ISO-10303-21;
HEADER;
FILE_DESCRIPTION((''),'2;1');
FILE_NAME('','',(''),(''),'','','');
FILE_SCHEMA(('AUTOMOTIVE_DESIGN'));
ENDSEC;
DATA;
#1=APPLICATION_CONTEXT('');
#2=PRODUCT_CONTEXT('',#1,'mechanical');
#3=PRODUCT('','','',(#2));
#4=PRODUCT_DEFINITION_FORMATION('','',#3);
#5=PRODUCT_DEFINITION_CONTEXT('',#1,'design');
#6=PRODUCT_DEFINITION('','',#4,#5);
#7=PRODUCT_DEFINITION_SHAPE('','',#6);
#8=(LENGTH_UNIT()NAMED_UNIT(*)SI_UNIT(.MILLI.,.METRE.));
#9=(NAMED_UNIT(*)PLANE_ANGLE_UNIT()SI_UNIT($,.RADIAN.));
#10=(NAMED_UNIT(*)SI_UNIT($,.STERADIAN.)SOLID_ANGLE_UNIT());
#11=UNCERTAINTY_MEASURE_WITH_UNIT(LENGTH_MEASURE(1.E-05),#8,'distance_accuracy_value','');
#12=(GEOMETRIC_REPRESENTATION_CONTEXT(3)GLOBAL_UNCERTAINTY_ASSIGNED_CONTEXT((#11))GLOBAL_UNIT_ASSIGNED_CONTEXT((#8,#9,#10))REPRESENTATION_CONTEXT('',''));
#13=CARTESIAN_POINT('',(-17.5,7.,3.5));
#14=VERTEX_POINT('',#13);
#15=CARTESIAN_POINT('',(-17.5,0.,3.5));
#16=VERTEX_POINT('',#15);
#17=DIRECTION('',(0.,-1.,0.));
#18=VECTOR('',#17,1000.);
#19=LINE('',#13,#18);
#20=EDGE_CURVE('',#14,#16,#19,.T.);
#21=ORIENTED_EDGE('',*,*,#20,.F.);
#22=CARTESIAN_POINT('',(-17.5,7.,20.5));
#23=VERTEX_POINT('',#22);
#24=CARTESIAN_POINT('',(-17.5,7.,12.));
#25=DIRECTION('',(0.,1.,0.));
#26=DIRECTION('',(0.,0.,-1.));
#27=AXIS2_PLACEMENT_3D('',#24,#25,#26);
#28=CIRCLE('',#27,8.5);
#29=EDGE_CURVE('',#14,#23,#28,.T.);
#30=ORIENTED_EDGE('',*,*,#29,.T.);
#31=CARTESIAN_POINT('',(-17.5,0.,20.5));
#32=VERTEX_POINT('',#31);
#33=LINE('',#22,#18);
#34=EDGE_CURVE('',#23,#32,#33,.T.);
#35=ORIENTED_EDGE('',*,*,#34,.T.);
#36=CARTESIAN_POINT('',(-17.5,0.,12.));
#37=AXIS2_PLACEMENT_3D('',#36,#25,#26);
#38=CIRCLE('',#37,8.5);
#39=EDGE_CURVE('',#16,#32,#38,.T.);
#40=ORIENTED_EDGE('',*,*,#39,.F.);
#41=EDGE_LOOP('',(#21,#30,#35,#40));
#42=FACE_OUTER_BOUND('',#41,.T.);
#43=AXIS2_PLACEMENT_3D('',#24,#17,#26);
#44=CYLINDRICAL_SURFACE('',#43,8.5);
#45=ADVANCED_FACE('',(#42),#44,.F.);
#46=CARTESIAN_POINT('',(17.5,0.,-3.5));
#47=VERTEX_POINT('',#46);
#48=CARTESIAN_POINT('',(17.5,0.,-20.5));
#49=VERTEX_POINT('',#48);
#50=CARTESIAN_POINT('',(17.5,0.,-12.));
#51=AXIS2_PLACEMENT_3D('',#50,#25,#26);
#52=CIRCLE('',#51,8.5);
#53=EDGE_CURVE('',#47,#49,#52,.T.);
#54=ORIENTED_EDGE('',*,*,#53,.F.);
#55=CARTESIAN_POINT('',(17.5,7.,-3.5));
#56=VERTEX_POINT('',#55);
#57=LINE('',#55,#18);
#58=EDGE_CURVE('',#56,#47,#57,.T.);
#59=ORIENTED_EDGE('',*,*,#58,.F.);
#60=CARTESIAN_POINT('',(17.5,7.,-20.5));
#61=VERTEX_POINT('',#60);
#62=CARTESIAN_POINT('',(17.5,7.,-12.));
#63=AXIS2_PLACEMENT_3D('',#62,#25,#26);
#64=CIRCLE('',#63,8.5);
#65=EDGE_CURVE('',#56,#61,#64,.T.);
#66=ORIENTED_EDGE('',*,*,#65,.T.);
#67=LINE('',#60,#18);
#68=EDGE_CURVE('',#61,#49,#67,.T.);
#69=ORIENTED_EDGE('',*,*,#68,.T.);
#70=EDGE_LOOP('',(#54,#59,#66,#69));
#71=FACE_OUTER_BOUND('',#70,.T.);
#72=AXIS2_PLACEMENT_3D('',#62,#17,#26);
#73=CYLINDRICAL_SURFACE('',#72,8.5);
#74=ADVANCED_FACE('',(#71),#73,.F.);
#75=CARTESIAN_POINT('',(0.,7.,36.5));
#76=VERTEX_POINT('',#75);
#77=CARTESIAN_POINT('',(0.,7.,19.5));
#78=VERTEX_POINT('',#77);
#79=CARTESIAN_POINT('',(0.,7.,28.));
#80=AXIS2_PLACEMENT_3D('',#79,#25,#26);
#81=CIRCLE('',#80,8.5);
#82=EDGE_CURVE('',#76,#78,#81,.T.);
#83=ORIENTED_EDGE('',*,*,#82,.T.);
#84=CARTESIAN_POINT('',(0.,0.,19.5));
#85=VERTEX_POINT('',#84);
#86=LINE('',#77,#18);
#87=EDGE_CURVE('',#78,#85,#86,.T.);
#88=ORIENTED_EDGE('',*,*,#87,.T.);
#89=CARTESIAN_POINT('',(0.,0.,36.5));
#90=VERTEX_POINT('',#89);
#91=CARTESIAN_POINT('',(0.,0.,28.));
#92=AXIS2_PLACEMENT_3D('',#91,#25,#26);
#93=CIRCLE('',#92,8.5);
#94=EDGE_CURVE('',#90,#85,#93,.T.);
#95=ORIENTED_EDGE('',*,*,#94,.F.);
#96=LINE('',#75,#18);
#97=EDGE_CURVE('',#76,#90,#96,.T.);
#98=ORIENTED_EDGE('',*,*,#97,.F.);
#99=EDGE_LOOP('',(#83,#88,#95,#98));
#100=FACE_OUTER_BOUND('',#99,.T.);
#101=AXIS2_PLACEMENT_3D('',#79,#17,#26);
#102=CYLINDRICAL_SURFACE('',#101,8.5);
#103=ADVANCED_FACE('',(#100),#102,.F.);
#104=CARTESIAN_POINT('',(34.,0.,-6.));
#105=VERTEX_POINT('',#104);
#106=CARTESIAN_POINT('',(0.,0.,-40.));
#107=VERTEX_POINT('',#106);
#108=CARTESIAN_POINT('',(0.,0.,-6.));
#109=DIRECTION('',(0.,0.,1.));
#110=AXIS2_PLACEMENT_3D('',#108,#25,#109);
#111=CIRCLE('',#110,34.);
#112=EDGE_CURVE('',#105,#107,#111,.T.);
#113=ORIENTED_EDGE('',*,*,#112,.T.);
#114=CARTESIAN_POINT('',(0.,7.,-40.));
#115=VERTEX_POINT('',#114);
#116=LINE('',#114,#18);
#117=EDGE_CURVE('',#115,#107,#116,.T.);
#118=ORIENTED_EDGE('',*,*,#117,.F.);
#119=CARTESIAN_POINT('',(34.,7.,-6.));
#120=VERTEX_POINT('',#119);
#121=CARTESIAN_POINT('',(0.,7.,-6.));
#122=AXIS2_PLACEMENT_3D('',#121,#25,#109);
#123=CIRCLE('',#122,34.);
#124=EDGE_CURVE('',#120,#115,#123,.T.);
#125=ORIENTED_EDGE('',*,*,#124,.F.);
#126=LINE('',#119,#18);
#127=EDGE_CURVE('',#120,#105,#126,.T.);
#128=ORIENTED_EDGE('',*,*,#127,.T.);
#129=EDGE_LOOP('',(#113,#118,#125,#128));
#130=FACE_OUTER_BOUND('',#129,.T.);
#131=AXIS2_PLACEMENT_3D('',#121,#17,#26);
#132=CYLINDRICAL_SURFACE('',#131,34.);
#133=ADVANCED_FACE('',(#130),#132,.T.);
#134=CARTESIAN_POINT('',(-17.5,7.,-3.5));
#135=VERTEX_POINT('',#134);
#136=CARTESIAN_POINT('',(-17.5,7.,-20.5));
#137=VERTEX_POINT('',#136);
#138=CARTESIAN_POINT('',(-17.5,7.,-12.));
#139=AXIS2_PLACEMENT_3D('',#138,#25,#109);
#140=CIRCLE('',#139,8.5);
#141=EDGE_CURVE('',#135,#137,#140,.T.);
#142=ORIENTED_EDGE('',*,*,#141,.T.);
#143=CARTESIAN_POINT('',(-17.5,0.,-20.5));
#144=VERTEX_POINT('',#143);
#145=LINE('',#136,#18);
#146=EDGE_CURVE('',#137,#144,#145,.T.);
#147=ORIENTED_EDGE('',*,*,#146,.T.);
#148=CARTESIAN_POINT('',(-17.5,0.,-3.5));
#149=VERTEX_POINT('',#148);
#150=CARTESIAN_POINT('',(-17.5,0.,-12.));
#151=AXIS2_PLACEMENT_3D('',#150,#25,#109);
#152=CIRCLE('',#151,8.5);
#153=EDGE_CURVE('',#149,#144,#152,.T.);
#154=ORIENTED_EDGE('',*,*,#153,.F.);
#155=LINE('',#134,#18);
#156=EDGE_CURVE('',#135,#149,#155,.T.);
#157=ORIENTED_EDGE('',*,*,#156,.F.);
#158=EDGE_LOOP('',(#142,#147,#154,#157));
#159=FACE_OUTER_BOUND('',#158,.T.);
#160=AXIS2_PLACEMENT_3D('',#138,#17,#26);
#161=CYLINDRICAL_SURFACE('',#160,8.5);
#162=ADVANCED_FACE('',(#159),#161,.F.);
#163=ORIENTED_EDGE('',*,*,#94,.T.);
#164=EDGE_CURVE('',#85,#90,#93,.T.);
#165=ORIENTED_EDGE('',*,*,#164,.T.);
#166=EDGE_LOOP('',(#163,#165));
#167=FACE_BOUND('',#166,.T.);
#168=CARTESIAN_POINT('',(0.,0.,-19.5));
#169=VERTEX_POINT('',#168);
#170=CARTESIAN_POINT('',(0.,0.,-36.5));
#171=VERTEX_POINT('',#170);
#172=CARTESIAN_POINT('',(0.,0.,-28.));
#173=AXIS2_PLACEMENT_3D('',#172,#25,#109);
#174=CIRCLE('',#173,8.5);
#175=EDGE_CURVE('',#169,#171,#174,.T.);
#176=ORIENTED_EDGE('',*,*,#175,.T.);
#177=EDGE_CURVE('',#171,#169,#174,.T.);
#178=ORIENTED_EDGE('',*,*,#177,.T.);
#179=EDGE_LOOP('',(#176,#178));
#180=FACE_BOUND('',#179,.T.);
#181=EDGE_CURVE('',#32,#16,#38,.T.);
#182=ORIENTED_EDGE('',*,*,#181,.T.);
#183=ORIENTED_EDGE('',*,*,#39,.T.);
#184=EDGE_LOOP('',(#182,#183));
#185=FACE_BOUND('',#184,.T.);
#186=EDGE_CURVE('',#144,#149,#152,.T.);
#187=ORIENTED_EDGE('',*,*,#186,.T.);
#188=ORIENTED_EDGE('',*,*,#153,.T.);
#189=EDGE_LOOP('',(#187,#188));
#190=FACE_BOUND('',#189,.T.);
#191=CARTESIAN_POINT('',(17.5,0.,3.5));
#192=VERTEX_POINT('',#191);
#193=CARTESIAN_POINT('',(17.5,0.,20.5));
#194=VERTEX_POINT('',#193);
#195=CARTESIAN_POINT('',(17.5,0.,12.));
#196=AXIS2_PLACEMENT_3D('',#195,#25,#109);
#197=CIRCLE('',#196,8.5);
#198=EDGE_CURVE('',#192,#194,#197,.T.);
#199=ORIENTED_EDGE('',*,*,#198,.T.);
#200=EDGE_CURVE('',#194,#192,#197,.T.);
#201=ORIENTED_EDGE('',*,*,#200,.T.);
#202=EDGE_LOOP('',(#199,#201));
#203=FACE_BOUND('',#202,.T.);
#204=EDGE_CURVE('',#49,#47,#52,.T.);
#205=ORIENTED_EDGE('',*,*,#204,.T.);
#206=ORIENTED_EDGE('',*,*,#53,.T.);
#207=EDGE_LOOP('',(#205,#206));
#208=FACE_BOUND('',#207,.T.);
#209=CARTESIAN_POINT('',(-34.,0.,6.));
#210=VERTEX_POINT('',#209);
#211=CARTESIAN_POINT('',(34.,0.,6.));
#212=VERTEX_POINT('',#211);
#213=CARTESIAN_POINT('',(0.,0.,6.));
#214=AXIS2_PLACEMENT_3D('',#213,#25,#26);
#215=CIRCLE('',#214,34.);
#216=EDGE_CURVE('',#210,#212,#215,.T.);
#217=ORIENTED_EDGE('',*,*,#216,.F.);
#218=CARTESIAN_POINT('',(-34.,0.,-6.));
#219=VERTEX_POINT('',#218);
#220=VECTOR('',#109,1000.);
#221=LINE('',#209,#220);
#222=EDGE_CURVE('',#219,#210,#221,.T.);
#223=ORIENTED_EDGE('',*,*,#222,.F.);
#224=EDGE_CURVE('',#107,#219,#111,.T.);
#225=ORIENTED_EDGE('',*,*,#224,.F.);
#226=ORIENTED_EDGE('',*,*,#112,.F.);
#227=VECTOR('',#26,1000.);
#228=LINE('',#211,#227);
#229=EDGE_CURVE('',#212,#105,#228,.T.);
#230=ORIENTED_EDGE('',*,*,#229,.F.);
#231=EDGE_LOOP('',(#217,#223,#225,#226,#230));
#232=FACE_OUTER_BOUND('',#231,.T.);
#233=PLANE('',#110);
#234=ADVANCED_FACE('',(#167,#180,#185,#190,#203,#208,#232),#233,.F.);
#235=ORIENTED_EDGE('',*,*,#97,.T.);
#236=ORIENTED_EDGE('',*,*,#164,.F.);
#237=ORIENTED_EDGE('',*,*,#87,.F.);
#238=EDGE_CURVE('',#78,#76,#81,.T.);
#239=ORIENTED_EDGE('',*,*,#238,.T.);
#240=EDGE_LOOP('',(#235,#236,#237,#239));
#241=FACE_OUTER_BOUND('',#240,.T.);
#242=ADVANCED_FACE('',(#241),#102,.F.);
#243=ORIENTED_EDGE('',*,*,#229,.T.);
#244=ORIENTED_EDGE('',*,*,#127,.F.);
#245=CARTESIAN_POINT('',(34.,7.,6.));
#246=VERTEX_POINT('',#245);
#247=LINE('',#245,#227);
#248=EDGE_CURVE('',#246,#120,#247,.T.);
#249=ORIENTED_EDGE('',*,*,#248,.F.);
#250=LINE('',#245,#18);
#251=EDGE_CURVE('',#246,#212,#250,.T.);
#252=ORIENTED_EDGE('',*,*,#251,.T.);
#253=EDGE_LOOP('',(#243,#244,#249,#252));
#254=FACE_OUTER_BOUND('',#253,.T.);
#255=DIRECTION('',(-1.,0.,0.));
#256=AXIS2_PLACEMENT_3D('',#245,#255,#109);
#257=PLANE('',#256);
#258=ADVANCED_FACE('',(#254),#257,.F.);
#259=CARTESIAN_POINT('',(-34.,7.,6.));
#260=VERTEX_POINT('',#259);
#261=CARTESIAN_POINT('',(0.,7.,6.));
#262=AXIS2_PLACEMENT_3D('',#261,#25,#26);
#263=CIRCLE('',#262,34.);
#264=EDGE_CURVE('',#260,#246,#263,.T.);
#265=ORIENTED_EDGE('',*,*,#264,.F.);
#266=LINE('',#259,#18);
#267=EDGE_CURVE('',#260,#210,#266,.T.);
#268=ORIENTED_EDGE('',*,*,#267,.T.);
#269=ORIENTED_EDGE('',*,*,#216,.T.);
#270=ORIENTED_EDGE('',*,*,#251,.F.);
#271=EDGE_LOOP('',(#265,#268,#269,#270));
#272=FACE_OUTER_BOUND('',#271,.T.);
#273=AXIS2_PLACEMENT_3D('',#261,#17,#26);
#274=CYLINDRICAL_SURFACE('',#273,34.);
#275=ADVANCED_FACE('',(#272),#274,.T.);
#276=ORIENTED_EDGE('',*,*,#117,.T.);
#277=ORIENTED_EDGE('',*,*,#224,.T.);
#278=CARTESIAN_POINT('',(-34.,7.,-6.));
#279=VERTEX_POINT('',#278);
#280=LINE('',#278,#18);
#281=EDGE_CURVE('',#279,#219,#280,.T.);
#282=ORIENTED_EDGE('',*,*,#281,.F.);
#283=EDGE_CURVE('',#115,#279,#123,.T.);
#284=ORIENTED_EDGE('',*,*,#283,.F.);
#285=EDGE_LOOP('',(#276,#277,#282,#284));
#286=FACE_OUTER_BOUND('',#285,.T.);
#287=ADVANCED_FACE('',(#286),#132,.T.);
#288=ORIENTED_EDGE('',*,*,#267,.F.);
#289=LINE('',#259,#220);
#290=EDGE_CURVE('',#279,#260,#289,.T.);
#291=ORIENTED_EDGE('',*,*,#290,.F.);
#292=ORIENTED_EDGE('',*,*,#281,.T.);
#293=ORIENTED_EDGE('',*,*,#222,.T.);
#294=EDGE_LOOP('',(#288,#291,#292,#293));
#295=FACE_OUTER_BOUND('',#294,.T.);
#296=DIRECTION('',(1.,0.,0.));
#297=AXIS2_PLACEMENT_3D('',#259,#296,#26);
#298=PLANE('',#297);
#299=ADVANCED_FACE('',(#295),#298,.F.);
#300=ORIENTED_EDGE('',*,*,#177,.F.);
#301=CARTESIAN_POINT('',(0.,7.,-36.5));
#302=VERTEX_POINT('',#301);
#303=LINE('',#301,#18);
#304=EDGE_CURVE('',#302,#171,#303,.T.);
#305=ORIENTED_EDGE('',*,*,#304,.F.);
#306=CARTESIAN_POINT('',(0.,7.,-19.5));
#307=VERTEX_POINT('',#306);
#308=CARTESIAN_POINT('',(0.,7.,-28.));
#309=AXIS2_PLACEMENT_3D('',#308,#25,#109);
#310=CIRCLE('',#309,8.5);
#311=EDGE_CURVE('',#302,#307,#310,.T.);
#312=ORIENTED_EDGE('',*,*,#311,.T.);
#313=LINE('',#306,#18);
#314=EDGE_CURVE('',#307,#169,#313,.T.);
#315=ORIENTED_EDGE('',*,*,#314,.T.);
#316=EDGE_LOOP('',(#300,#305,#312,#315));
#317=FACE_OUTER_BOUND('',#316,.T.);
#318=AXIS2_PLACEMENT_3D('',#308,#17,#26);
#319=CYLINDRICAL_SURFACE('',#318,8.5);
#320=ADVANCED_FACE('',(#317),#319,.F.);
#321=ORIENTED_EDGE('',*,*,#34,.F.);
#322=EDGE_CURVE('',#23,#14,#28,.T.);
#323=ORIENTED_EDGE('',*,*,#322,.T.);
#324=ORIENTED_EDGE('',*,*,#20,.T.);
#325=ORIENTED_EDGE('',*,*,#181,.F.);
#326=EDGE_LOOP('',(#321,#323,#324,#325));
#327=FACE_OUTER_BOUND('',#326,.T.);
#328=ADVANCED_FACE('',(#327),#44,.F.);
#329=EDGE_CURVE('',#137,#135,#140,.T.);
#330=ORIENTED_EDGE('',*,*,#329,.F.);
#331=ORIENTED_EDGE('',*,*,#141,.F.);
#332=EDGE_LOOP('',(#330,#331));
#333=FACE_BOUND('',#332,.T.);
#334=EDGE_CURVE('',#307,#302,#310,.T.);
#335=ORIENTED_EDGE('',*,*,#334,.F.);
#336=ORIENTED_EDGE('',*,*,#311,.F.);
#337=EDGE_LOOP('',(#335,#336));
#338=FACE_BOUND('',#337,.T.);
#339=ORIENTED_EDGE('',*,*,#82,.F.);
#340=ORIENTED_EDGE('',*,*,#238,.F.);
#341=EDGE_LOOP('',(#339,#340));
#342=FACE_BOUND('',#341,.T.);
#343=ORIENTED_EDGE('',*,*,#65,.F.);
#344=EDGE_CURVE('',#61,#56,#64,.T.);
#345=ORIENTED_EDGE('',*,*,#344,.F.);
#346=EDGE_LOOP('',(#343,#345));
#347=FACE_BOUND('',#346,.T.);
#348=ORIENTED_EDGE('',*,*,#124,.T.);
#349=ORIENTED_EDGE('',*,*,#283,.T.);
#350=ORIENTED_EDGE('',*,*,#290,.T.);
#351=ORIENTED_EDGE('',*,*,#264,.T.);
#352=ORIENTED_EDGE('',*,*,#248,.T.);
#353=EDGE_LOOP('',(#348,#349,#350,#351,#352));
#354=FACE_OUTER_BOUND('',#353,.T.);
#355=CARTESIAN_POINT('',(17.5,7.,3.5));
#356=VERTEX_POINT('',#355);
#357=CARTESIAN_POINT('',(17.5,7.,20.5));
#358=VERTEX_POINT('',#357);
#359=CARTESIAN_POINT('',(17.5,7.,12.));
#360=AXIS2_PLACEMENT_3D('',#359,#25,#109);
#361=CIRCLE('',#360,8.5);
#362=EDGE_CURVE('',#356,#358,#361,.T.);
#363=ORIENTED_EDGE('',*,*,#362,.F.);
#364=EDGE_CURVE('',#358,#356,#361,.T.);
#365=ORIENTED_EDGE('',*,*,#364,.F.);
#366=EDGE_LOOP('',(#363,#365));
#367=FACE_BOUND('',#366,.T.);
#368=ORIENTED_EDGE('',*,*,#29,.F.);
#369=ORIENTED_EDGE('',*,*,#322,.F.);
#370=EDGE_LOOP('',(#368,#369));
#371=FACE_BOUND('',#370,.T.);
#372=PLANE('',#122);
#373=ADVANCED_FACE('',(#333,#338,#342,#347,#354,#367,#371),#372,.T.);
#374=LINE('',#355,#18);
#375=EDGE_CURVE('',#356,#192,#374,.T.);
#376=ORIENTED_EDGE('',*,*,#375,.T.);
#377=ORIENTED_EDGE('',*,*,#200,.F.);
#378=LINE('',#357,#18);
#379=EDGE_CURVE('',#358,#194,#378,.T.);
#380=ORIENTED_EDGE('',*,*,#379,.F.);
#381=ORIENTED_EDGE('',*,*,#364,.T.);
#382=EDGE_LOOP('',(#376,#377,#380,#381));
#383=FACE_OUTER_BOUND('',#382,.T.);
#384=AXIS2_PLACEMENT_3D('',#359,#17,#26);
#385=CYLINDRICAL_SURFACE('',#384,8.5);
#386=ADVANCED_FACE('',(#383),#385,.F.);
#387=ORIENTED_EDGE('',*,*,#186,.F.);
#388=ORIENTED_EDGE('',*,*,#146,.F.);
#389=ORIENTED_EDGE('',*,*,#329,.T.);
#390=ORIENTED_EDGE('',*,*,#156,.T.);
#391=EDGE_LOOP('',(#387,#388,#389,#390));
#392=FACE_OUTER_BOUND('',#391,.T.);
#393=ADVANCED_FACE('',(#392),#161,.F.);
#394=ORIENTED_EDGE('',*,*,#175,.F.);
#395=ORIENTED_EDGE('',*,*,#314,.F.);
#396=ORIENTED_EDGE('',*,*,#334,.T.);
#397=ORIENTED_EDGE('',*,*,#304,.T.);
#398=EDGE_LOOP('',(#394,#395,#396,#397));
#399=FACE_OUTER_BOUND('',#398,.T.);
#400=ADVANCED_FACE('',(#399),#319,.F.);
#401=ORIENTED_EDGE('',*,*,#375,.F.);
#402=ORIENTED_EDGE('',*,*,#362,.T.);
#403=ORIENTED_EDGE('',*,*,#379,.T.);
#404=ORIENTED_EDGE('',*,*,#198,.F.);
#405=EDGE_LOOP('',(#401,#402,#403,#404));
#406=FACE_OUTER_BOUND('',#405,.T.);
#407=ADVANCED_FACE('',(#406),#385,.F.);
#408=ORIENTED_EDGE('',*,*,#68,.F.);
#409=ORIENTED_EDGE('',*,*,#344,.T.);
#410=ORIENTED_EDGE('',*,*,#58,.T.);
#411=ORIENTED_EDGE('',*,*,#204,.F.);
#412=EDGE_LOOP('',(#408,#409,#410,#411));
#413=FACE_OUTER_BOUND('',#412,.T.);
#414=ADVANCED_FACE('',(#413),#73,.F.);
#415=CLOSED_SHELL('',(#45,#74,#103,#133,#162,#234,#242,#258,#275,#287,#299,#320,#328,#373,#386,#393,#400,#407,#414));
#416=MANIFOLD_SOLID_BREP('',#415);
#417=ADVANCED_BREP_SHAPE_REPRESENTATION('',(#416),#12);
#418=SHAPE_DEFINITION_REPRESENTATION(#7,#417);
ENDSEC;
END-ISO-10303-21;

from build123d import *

# Parameters (mm, degrees)
SKETCH_1_R      = 8.5
EXTRUDE_1_DEPTH = 7


with BuildPart() as part:
    # 草图1 → 凸台-拉伸1 (new body)
    with BuildSketch(Plane(origin=(0, 0, 0), x_dir=(1, 0, 0), z_dir=(0, 1, 0))):
        with BuildLine():
            Line((34, -6), (34, 6))
            ThreePointArc((34, 6), (0, 40), (-34, 6))
            Line((-34, 6), (-34, -6))
            ThreePointArc((-34, -6), (0, -40), (34, -6))
        make_face()
        with Locations(Location((0, 28, 0), (0, 0, 270))):
            Circle(SKETCH_1_R, mode=Mode.SUBTRACT)
        with Locations(Location((-17.5, 12, 0), (0, 0, 270))):
            Circle(SKETCH_1_R, mode=Mode.SUBTRACT)
        with Locations(Location((17.5, 12, 0), (0, 0, 90))):
            Circle(SKETCH_1_R, mode=Mode.SUBTRACT)
        with Locations(Location((17.5, -12, 0), (0, 0, 270))):
            Circle(SKETCH_1_R, mode=Mode.SUBTRACT)
        with Locations(Location((-17.5, -12, 0), (0, 0, 90))):
            Circle(SKETCH_1_R, mode=Mode.SUBTRACT)
        with Locations(Location((0, -28, 0), (0, 0, 90))):
            Circle(SKETCH_1_R, mode=Mode.SUBTRACT)
    extrude(amount=EXTRUDE_1_DEPTH)


solid = part.part
